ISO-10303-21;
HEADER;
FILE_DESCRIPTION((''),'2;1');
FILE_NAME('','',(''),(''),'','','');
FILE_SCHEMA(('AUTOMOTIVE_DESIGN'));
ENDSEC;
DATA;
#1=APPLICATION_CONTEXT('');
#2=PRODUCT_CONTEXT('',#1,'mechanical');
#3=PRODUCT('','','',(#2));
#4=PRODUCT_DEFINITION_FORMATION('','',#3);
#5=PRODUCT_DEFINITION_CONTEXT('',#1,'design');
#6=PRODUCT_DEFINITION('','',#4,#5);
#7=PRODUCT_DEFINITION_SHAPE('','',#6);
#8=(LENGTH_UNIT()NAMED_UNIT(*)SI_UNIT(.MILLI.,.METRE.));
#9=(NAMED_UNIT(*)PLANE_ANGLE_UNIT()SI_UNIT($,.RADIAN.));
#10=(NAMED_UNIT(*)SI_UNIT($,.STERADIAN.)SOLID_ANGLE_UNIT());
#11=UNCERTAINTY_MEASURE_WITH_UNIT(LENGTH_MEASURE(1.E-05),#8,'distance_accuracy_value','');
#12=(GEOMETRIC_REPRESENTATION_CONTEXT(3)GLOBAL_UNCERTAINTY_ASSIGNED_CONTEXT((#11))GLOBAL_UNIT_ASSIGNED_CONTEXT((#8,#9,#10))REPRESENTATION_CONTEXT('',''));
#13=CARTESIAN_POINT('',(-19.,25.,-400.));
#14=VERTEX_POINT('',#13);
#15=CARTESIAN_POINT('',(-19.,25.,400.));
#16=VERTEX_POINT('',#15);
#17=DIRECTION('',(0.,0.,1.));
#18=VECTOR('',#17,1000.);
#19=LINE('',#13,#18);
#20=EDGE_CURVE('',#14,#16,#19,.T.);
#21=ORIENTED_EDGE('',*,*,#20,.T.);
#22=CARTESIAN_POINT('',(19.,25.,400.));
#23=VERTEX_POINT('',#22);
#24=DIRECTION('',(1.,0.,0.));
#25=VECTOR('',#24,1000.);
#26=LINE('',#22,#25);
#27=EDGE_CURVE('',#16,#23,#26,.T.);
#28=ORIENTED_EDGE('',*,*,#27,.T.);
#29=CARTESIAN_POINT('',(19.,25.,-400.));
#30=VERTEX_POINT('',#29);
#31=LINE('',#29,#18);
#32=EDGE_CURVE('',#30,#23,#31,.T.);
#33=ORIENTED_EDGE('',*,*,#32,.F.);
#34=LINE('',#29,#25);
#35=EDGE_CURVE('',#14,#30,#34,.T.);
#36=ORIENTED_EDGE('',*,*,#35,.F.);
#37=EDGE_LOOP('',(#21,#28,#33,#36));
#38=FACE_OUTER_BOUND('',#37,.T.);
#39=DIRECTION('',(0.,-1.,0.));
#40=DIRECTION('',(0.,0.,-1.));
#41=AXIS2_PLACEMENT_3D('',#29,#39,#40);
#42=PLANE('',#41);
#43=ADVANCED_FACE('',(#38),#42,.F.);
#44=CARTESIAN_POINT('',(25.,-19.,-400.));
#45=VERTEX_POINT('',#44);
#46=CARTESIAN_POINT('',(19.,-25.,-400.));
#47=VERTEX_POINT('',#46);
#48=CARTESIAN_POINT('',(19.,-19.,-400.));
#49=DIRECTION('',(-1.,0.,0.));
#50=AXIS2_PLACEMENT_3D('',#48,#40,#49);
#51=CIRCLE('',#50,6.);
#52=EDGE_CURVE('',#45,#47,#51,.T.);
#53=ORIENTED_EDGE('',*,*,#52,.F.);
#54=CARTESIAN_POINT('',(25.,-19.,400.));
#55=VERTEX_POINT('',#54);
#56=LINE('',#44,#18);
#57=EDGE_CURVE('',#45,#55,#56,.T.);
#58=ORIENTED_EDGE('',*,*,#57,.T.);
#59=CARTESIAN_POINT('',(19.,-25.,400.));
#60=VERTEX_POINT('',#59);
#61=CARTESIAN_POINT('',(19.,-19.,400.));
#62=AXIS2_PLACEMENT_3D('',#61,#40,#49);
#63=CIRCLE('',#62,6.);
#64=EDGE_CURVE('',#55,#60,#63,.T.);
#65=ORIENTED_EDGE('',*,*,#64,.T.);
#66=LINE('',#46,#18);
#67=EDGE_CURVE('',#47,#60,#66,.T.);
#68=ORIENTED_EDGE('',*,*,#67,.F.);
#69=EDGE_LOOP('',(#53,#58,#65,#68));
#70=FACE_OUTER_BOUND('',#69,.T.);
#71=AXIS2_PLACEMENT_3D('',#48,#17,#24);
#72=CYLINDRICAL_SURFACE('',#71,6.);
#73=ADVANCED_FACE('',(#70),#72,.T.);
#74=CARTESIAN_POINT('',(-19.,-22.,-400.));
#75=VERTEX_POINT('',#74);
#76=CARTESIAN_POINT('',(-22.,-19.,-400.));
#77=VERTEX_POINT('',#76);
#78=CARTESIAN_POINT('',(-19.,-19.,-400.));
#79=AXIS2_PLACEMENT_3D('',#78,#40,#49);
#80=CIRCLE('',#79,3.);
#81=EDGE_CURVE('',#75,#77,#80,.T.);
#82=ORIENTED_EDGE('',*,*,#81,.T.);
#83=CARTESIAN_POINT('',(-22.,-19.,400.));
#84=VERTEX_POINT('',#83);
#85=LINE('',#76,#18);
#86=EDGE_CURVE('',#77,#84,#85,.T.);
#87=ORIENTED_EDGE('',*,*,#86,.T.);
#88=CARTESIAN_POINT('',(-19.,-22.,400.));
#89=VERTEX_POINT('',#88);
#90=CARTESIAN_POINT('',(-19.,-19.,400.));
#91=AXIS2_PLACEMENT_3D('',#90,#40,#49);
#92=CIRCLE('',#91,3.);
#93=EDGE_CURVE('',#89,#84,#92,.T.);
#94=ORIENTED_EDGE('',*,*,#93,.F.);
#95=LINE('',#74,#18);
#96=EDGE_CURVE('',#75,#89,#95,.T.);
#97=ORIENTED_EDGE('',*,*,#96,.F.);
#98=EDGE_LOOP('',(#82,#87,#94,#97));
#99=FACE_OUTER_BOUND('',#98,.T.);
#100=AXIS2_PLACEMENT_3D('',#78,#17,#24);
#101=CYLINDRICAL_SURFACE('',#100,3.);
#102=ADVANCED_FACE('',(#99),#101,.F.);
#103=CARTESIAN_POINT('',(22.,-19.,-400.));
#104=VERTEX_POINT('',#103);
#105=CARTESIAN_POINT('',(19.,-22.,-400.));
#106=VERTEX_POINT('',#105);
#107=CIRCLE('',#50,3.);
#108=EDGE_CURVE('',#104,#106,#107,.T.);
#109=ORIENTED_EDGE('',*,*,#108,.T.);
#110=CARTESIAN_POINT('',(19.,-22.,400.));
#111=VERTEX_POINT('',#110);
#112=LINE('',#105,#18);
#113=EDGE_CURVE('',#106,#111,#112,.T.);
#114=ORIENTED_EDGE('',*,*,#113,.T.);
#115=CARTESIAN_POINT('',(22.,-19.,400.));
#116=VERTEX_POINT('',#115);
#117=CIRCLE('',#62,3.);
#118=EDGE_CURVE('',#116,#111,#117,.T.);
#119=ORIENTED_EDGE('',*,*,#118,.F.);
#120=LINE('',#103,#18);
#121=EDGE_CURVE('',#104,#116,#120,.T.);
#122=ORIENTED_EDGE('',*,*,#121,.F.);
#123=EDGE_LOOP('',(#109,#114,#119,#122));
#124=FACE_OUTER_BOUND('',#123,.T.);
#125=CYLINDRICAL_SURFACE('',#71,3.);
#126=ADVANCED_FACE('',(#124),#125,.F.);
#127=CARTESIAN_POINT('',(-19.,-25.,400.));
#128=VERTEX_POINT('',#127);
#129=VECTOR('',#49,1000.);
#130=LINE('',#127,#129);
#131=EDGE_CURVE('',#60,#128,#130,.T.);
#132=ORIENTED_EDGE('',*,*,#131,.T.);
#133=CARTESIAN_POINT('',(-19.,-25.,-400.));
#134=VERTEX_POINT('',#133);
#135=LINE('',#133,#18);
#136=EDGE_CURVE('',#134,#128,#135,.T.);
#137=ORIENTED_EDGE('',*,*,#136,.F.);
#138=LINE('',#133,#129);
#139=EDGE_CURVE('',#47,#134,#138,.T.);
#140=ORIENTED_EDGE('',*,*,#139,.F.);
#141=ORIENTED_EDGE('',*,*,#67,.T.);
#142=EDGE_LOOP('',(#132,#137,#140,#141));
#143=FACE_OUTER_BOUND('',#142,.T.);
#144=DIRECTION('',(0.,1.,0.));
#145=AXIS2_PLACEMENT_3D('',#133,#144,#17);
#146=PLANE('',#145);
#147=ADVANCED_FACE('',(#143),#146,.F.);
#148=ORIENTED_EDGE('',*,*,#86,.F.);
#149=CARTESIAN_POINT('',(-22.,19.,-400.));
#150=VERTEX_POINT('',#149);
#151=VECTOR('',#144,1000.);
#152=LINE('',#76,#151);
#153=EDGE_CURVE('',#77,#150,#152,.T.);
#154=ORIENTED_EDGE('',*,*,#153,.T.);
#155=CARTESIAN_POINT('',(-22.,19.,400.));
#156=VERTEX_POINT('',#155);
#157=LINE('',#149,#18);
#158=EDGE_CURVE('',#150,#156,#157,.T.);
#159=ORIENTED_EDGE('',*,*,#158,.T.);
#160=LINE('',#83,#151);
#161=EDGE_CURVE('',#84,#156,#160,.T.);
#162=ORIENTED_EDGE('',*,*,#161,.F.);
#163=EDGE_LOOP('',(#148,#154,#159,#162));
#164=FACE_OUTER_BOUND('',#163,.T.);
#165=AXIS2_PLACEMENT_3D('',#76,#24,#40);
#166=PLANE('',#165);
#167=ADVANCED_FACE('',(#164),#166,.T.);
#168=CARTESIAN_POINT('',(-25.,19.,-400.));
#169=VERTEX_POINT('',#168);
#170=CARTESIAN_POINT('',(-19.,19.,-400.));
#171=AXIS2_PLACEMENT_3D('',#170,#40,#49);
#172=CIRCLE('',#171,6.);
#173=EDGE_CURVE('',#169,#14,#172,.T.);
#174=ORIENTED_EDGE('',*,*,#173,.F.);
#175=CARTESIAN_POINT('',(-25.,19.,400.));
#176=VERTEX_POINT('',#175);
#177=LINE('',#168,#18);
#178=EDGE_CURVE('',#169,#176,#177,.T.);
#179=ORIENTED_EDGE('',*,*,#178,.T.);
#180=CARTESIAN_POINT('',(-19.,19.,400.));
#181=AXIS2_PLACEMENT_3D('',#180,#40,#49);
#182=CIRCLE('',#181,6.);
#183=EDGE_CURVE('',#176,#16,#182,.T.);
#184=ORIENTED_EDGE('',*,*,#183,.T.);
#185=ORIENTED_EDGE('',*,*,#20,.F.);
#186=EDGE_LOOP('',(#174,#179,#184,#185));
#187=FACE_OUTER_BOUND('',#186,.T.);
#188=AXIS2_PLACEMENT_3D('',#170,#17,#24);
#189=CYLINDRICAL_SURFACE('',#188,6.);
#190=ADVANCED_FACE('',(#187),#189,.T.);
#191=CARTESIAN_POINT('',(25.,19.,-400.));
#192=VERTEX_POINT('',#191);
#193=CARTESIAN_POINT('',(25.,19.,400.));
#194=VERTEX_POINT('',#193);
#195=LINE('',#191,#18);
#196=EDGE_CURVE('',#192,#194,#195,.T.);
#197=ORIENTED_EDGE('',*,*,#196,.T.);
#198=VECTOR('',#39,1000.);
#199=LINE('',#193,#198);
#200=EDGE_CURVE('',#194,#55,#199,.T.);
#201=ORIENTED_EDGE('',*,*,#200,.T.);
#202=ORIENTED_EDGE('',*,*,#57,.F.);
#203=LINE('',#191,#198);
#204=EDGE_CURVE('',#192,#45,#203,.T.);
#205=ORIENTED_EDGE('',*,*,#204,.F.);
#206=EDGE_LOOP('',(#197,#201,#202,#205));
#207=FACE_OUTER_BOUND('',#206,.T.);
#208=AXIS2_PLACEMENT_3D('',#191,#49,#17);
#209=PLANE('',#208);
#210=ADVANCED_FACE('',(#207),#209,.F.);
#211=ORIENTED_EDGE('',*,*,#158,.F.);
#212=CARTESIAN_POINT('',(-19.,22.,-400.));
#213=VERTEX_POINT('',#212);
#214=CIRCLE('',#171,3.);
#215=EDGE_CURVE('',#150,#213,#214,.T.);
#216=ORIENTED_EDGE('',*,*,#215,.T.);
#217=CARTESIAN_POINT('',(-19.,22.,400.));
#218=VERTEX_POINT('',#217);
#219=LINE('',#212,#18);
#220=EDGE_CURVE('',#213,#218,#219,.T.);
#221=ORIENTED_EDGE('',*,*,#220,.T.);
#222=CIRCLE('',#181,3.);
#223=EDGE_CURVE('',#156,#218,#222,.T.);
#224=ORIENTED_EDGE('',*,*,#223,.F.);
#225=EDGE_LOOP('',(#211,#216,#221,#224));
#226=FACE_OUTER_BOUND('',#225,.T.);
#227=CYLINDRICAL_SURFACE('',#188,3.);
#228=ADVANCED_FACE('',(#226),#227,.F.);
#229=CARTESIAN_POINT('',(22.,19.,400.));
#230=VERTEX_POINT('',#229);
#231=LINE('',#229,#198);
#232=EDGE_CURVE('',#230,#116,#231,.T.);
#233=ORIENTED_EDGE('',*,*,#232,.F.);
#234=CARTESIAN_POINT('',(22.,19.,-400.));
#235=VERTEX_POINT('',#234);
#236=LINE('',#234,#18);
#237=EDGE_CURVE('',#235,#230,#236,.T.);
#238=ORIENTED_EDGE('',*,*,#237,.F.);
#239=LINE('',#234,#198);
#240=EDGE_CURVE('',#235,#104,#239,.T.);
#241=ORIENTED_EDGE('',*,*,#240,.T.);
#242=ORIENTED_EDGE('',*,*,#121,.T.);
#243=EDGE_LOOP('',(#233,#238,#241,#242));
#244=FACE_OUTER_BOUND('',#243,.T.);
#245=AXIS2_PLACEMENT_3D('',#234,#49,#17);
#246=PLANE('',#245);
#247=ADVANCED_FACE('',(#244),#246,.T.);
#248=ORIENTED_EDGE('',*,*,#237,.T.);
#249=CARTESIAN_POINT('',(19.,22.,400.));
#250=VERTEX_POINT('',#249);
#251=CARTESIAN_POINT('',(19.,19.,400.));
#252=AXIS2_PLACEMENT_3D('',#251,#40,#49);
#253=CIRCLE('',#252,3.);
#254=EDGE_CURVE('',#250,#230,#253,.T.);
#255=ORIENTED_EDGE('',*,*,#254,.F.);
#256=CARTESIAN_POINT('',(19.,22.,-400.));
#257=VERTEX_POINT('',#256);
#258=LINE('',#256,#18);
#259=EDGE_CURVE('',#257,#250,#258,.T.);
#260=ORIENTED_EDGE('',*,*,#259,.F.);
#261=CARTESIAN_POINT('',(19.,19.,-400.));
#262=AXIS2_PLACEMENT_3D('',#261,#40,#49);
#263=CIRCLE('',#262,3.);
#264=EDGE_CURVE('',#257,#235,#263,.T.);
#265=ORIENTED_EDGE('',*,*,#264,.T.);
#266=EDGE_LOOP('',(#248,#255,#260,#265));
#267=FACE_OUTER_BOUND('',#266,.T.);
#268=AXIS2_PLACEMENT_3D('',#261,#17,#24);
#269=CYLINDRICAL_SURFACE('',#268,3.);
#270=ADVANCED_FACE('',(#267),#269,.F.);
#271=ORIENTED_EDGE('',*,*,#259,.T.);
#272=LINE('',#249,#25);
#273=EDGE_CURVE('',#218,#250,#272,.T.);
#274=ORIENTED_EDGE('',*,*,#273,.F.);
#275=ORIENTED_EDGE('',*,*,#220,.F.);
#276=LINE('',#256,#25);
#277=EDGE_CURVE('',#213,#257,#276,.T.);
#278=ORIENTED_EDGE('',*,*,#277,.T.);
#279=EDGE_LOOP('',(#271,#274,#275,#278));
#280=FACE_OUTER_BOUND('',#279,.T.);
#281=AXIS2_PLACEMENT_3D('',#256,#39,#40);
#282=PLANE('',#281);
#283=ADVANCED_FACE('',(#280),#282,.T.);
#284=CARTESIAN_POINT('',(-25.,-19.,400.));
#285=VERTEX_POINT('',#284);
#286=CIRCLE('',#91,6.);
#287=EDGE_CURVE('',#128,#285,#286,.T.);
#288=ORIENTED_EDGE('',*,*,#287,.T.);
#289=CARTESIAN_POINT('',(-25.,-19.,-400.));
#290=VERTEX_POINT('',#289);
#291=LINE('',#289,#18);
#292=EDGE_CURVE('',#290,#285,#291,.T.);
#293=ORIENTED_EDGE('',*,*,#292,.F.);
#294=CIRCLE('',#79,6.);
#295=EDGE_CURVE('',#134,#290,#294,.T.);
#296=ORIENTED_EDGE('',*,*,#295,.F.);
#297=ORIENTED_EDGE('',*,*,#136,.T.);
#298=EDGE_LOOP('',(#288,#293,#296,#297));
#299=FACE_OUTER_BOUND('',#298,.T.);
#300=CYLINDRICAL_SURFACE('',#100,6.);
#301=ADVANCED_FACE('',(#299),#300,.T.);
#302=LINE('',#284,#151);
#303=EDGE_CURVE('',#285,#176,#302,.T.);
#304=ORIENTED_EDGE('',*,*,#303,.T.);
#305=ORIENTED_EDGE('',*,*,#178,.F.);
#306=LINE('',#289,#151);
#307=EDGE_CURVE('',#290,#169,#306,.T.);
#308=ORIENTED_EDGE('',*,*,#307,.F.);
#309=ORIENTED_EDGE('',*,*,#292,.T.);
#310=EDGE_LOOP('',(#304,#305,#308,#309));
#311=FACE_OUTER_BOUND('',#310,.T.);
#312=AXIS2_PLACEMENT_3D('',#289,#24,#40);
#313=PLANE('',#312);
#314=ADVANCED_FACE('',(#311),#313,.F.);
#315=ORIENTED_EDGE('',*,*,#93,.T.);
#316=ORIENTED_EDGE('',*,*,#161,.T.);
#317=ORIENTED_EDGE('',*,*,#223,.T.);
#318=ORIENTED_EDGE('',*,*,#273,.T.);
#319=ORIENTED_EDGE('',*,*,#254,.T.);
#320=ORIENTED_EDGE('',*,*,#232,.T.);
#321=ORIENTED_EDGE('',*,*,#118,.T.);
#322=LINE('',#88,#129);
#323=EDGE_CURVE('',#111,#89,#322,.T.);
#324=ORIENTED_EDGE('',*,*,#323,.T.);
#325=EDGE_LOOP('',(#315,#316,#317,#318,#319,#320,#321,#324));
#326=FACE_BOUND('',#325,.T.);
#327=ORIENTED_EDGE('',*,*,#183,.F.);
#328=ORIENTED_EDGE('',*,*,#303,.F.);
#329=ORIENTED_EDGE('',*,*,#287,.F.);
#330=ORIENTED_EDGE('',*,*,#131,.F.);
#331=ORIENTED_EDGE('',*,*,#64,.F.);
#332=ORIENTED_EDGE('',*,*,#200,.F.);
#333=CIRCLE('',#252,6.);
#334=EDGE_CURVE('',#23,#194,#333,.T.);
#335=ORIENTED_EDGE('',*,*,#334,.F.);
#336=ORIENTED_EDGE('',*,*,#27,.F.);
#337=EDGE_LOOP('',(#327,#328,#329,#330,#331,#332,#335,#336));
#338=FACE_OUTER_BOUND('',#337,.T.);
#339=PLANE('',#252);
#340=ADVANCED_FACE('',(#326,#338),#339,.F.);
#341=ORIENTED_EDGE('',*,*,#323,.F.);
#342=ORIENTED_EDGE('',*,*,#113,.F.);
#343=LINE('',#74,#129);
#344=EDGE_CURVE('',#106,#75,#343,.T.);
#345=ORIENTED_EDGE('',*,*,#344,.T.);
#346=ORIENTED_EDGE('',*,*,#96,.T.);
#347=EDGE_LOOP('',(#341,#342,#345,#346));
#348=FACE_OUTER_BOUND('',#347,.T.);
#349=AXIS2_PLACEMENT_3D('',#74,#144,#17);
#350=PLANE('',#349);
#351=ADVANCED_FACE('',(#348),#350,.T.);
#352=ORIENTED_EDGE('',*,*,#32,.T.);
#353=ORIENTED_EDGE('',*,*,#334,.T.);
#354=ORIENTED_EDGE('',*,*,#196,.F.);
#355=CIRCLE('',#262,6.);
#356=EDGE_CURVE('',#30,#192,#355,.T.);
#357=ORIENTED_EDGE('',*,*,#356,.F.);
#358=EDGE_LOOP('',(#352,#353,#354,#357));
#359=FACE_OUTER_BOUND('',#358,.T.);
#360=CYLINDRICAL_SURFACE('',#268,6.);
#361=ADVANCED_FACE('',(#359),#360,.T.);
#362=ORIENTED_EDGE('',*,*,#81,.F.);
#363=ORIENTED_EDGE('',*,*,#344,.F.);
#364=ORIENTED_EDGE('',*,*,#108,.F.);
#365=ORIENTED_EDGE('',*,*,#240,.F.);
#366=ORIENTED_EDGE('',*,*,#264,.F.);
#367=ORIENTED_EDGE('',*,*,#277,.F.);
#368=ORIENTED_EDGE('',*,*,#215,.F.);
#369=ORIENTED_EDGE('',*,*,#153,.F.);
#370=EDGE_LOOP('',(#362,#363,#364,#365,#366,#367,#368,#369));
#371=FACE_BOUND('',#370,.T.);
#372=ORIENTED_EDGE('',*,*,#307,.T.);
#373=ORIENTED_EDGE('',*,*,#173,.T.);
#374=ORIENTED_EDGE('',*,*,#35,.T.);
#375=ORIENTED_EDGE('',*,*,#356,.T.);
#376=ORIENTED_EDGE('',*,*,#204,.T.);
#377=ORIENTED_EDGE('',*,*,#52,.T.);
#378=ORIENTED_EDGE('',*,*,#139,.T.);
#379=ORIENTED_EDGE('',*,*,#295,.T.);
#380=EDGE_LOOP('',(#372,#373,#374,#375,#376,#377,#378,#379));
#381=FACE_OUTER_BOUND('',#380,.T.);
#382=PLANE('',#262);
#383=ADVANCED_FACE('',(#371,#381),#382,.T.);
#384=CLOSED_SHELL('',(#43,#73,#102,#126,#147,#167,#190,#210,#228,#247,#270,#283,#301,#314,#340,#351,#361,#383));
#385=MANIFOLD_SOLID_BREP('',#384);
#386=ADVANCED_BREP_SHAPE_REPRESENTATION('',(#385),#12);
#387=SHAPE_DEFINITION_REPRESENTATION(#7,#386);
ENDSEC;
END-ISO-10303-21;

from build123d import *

# Parameters (mm, degrees)
GB_6728_1986_050_X_50_X_3_1_DEPTH = 800


with BuildPart() as part:
    # Sketch1 → Gb／6728-1986方形空心型钢 050 X 50 X 3(1) (new body)
    with BuildSketch(Plane.YX.offset(-400)):
        with BuildLine():
            Line((-19, -25), (19, -25))
            ThreePointArc((19, -25), (23.242640687, -23.242640687), (25, -19))
            Line((25, -19), (25, 19))
            ThreePointArc((25, 19), (23.242640687, 23.242640687), (19, 25))
            Line((19, 25), (-19, 25))
            ThreePointArc((-19, 25), (-23.242640687, 23.242640687), (-25, 19))
            Line((-25, 19), (-25, -19))
            ThreePointArc((-25, -19), (-23.242640687, -23.242640687), (-19, -25))
        make_face()
        with BuildLine():
            Line((-19, -22), (19, -22))
            ThreePointArc((19, -22), (21.121320344, -21.121320344), (22, -19))
            Line((22, -19), (22, 19))
            ThreePointArc((22, 19), (21.121320344, 21.121320344), (19, 22))
            Line((19, 22), (-19, 22))
            ThreePointArc((-19, 22), (-21.121320344, 21.121320344), (-22, 19))
            Line((-22, 19), (-22, -19))
            ThreePointArc((-22, -19), (-21.121320344, -21.121320344), (-19, -22))
        make_face(mode=Mode.SUBTRACT)
    extrude(amount=GB_6728_1986_050_X_50_X_3_1_DEPTH)


solid = part.part
